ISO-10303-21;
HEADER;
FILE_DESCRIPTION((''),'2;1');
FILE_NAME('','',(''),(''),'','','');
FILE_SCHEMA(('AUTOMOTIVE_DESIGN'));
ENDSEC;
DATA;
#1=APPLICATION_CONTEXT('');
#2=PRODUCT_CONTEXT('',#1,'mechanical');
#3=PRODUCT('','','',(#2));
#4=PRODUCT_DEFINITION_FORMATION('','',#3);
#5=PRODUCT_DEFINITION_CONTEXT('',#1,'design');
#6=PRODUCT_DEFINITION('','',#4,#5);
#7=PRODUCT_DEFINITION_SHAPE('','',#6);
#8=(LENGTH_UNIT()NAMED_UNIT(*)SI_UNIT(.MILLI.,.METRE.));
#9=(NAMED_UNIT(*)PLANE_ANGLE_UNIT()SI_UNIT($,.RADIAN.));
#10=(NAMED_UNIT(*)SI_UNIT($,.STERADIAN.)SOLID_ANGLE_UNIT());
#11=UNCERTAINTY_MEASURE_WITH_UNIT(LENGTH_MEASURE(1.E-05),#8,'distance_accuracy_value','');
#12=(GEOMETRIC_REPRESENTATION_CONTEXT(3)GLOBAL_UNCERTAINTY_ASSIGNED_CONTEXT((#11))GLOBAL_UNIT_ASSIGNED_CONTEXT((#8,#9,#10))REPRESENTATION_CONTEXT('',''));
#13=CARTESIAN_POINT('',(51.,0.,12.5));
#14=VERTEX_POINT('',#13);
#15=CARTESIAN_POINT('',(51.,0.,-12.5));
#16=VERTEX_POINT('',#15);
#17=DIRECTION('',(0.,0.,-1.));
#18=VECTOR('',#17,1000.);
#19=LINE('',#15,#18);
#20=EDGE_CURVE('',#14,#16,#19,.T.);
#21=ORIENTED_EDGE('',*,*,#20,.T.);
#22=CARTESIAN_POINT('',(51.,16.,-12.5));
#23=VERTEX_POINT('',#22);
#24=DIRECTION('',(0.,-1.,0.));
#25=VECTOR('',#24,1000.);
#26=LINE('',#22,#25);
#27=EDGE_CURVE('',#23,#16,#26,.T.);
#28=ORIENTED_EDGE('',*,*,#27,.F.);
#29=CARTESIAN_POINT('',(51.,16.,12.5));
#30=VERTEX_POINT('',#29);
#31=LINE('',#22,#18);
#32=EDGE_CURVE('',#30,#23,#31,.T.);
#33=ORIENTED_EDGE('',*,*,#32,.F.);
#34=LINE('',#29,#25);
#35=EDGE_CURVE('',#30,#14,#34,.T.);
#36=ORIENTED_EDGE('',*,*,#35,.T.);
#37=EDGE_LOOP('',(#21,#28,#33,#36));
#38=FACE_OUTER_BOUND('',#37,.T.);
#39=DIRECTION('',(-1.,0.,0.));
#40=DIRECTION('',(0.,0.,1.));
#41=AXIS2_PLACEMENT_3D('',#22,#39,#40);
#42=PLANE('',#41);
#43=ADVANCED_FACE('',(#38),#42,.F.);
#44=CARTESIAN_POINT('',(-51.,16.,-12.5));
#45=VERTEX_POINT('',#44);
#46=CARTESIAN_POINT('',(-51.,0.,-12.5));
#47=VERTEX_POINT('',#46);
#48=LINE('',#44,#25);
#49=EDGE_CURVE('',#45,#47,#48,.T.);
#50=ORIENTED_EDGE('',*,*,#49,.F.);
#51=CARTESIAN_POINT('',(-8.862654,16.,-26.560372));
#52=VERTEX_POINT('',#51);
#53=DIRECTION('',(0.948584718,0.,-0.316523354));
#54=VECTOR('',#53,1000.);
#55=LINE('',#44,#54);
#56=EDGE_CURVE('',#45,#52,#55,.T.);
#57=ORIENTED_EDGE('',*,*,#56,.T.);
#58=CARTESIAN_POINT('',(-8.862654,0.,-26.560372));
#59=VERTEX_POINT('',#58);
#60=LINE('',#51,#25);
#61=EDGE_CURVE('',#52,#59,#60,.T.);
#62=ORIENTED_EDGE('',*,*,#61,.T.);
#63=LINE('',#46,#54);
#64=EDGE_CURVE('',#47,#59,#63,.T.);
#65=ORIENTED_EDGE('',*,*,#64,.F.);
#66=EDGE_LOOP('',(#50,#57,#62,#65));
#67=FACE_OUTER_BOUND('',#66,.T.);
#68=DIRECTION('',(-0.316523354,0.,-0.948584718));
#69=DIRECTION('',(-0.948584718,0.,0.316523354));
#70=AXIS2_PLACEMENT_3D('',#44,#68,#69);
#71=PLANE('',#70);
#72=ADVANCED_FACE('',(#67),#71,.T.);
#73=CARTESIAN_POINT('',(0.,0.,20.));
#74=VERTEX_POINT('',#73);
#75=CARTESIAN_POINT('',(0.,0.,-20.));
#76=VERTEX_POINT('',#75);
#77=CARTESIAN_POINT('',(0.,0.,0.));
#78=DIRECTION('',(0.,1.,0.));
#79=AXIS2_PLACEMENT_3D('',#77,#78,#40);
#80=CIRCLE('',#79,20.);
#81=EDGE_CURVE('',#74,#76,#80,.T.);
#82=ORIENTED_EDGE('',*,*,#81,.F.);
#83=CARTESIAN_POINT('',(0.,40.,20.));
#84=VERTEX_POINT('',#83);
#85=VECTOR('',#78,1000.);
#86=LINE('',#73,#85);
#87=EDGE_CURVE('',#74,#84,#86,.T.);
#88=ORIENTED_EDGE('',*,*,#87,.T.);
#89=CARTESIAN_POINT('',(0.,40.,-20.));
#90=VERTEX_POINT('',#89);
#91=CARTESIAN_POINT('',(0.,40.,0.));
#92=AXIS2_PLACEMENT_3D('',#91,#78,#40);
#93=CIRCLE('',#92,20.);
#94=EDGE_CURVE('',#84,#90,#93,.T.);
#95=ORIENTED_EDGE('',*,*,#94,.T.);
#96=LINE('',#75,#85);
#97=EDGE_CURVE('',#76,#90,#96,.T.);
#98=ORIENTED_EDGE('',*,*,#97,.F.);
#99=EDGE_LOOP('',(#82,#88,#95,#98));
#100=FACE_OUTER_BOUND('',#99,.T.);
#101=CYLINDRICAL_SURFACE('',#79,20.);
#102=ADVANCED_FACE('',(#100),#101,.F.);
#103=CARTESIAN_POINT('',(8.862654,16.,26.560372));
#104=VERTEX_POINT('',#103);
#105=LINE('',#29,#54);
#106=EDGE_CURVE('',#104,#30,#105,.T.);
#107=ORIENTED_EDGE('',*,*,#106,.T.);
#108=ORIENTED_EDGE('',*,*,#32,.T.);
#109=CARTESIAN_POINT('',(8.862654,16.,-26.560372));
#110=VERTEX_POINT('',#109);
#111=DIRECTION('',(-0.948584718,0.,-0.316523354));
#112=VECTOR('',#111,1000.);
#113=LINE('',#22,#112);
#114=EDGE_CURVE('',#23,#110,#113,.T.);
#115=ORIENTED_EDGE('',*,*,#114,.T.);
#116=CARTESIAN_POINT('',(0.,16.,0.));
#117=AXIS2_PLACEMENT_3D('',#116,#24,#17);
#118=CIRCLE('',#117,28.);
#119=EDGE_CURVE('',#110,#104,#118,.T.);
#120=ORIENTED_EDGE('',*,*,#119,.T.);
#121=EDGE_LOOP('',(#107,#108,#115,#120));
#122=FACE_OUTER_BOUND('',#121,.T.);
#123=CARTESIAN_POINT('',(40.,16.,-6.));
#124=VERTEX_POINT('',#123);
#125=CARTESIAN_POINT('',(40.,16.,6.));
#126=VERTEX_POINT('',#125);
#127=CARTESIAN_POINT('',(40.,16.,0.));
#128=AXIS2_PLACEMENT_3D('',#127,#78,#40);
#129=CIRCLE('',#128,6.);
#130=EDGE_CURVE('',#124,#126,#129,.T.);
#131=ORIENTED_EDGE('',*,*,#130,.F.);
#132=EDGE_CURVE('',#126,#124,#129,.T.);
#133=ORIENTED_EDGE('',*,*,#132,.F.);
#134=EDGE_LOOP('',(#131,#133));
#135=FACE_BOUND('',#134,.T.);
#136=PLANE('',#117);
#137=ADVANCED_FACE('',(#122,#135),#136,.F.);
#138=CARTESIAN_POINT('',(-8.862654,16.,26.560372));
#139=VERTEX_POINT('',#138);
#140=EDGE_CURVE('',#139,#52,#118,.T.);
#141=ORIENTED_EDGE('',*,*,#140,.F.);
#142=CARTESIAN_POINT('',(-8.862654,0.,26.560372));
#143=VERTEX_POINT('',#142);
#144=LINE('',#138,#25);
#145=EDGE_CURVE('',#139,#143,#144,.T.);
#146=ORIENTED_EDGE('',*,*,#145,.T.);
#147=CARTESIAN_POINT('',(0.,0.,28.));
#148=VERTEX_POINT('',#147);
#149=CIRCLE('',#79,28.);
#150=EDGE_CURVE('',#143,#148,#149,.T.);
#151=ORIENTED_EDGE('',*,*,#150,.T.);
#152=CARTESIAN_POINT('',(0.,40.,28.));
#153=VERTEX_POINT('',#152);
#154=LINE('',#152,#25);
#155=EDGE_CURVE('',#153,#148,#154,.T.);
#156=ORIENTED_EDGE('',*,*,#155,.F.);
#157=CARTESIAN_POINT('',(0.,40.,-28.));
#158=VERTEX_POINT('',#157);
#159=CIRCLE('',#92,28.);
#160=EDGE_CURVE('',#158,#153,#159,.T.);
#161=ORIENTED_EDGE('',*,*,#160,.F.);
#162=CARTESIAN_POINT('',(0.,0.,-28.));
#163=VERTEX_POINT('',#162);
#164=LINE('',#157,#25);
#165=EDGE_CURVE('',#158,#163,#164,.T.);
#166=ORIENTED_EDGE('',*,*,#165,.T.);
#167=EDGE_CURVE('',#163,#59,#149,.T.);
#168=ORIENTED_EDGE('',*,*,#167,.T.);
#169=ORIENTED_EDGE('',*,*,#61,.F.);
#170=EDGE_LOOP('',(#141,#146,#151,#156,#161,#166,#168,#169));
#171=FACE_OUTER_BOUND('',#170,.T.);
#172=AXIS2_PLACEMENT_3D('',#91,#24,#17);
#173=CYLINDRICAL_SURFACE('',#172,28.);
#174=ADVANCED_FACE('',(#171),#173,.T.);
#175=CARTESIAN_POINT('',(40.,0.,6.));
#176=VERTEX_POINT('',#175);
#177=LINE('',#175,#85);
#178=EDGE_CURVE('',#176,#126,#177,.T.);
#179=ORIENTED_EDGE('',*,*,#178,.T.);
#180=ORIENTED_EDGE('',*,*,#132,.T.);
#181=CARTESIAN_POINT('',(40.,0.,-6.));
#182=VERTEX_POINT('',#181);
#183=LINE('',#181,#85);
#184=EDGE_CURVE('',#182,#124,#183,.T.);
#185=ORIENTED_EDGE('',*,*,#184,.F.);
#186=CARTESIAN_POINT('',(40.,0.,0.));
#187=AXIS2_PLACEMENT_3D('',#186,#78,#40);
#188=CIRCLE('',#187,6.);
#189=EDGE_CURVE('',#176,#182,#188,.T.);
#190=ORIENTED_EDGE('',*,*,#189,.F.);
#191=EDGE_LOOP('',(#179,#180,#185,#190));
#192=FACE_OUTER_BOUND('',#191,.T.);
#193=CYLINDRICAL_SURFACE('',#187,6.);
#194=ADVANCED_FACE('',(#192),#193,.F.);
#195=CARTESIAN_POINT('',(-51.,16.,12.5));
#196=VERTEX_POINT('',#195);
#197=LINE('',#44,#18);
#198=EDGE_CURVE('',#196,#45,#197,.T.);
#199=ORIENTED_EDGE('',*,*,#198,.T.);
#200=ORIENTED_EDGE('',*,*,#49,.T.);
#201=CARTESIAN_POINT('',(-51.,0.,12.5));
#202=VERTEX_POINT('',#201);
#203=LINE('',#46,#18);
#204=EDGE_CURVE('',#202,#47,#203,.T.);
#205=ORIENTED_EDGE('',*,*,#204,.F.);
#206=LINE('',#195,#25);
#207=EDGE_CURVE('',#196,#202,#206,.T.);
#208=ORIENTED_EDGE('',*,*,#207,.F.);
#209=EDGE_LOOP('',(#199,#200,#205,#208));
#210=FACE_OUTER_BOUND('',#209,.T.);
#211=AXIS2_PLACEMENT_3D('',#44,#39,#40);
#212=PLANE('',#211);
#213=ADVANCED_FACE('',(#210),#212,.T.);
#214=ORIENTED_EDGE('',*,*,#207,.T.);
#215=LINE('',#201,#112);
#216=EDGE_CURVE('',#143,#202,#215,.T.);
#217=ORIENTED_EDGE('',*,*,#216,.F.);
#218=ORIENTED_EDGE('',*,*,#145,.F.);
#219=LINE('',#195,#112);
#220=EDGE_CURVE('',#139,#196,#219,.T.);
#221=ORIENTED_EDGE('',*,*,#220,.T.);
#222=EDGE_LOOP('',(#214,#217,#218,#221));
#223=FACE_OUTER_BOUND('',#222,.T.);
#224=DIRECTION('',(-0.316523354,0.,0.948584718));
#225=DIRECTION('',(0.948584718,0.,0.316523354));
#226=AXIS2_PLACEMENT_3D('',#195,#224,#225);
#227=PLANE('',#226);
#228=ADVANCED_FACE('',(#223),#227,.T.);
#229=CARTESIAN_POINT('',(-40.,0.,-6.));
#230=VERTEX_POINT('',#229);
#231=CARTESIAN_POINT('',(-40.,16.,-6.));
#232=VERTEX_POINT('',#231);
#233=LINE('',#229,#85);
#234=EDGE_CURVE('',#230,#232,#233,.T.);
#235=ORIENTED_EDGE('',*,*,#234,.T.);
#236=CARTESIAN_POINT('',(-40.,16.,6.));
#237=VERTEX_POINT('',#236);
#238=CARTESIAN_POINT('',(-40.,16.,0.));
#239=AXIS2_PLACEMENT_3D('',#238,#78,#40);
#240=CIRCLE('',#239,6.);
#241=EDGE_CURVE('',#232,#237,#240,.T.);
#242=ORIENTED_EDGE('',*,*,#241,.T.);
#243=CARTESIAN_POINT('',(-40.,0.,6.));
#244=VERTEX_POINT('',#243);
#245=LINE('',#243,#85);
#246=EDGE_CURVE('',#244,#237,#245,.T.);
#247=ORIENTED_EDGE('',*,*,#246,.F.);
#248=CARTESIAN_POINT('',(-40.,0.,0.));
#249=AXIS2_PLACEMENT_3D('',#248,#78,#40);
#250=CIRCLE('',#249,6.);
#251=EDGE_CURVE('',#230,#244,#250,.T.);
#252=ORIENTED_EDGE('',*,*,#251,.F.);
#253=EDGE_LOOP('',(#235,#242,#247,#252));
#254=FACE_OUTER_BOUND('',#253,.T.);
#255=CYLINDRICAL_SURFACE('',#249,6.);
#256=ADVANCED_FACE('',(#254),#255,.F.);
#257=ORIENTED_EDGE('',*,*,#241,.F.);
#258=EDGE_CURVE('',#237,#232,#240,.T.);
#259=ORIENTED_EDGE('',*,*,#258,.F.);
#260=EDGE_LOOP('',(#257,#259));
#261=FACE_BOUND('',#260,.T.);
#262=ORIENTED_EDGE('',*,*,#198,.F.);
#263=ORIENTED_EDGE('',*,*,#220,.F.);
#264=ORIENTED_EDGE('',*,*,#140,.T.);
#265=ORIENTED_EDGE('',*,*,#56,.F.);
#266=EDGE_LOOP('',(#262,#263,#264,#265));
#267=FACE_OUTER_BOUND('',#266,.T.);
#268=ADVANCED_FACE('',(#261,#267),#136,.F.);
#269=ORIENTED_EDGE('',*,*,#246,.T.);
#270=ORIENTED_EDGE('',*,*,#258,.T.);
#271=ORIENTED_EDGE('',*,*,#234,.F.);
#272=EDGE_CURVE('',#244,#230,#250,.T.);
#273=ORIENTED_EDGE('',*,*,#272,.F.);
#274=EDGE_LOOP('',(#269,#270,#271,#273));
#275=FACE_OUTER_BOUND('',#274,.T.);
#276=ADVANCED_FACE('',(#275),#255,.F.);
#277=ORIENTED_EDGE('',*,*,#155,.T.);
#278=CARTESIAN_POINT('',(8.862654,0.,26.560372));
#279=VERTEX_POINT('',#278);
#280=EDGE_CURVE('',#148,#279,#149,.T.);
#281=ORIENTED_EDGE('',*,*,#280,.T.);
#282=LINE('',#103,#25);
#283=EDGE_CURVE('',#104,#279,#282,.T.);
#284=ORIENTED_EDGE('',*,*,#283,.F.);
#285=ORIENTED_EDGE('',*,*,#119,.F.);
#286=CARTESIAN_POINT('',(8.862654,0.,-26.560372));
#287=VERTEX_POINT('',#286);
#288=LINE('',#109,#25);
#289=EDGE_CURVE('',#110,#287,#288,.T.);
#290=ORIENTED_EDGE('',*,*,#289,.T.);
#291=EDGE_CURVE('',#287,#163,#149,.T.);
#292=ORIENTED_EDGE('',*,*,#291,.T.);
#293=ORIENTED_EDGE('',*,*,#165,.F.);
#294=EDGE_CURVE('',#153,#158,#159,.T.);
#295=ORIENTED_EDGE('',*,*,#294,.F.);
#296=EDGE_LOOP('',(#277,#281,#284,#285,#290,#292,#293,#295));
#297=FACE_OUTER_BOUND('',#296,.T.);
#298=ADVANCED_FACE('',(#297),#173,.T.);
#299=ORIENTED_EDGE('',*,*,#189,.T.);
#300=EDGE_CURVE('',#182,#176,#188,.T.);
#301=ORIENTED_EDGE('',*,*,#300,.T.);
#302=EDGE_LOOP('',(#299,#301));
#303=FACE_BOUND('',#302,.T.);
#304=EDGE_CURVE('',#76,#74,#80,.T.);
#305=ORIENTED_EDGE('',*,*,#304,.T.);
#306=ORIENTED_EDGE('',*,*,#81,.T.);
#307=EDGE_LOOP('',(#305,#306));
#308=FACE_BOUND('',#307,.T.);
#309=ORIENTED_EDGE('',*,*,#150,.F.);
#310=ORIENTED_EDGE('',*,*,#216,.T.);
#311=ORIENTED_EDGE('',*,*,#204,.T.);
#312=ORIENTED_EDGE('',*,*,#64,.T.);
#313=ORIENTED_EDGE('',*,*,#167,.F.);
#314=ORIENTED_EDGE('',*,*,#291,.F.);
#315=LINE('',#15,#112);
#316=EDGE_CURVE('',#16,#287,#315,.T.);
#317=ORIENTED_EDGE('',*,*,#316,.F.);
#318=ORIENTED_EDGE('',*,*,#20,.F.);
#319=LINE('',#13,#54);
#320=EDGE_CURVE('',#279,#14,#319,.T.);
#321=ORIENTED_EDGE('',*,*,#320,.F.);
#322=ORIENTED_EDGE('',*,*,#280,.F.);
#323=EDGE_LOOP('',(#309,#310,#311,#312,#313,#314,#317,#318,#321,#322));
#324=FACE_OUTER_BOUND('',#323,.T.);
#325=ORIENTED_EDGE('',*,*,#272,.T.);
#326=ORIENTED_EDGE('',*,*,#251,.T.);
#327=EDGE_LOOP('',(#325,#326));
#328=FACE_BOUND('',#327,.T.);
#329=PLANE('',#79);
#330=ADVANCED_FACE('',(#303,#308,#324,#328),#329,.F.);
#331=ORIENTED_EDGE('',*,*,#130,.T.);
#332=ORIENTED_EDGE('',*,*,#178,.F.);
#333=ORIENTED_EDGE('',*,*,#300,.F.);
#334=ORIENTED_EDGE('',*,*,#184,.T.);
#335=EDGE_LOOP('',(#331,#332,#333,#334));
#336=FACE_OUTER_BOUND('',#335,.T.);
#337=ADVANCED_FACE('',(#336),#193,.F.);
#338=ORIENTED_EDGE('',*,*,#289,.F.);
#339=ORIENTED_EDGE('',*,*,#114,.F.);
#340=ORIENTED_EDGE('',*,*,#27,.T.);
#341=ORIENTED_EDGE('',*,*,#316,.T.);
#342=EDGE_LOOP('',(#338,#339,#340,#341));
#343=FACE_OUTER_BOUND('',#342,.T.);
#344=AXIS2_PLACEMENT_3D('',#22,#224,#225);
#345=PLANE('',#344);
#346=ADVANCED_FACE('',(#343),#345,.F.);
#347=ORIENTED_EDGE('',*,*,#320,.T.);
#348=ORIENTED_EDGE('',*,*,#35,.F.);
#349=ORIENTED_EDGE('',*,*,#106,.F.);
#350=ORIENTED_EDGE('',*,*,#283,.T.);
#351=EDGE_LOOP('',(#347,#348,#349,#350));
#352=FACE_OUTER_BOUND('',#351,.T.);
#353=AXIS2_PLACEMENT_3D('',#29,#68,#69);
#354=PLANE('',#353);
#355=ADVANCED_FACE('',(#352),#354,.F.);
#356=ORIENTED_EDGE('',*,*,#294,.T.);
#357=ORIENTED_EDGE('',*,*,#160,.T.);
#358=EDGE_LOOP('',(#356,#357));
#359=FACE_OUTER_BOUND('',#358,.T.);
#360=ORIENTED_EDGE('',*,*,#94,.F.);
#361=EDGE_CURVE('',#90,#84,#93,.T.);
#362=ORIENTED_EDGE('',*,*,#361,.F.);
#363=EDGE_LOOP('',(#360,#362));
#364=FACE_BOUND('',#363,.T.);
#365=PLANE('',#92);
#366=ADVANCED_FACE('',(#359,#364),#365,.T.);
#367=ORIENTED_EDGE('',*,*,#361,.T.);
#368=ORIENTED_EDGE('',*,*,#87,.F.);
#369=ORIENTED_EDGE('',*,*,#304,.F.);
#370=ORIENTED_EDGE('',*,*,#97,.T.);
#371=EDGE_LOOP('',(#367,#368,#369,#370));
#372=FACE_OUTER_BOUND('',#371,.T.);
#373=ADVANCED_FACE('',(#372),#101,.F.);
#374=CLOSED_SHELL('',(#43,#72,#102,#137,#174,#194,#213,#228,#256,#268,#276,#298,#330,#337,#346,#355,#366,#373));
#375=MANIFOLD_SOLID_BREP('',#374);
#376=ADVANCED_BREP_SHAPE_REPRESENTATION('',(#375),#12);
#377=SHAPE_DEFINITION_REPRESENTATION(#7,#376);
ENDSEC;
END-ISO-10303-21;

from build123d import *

# Parameters (mm, degrees)
SKETCH_1_R          = 28
EXTRUDE_1_DEPTH     = 40
EXTRUDE_2_DEPTH     = 16
SKETCH_3_R          = 20
CUT_EXTRUDE_1_DEPTH = 71.604532432
SKETCH_4_R          = 6
CUT_EXTRUDE_2_DEPTH = 63.93647591


with BuildPart() as part:
    # 草图1 → 凸台-拉伸1 (new body)
    with BuildSketch(Plane(origin=(0, 0, 0), x_dir=(1, 0, 0), z_dir=(0, 1, 0))):
        with Locations(Location((0, 0, 0), (0, 0, 270))):
            Circle(SKETCH_1_R)
    extrude(amount=EXTRUDE_1_DEPTH)

    # 草图2 → 凸台-拉伸2 (add)
    with BuildSketch(Plane.XZ):
        Polygon((-51, -12.5), (-51, 12.5), (-8.862653898, 26.560372096), (-8.862653898, -26.560372096), align=None)
    extrude_2 = extrude(amount=-EXTRUDE_2_DEPTH)

    # 镜向1: 凸台-拉伸2 across plane
    add(extrude_2.mirror(Plane(origin=(0, 0, 0), x_dir=(0, 0, 1), z_dir=(1, 0, 0))))

    # 草图3 → 切除-拉伸1 (cut, through all)
    with BuildSketch(Plane(origin=(0, 40, 0), x_dir=(1, 0, 0), z_dir=(0, 1, 0))):
        with Locations(Location((0, 0, 0), (0, 0, 270))):
            Circle(SKETCH_3_R)
    extrude(amount=-CUT_EXTRUDE_1_DEPTH, mode=Mode.SUBTRACT)

    # 草图4 → 切除-拉伸2 (cut, through all)
    with BuildSketch(Plane(origin=(0, 16, 0), x_dir=(1, 0, 0), z_dir=(0, 1, 0))):
        with Locations(Location((-40, 0, 0), (0, 0, 270))):
            Circle(SKETCH_4_R)
        with Locations(Location((40, 0, 0), (0, 0, 270))):
            Circle(SKETCH_4_R)
    extrude(amount=-CUT_EXTRUDE_2_DEPTH, mode=Mode.SUBTRACT)


solid = part.part
